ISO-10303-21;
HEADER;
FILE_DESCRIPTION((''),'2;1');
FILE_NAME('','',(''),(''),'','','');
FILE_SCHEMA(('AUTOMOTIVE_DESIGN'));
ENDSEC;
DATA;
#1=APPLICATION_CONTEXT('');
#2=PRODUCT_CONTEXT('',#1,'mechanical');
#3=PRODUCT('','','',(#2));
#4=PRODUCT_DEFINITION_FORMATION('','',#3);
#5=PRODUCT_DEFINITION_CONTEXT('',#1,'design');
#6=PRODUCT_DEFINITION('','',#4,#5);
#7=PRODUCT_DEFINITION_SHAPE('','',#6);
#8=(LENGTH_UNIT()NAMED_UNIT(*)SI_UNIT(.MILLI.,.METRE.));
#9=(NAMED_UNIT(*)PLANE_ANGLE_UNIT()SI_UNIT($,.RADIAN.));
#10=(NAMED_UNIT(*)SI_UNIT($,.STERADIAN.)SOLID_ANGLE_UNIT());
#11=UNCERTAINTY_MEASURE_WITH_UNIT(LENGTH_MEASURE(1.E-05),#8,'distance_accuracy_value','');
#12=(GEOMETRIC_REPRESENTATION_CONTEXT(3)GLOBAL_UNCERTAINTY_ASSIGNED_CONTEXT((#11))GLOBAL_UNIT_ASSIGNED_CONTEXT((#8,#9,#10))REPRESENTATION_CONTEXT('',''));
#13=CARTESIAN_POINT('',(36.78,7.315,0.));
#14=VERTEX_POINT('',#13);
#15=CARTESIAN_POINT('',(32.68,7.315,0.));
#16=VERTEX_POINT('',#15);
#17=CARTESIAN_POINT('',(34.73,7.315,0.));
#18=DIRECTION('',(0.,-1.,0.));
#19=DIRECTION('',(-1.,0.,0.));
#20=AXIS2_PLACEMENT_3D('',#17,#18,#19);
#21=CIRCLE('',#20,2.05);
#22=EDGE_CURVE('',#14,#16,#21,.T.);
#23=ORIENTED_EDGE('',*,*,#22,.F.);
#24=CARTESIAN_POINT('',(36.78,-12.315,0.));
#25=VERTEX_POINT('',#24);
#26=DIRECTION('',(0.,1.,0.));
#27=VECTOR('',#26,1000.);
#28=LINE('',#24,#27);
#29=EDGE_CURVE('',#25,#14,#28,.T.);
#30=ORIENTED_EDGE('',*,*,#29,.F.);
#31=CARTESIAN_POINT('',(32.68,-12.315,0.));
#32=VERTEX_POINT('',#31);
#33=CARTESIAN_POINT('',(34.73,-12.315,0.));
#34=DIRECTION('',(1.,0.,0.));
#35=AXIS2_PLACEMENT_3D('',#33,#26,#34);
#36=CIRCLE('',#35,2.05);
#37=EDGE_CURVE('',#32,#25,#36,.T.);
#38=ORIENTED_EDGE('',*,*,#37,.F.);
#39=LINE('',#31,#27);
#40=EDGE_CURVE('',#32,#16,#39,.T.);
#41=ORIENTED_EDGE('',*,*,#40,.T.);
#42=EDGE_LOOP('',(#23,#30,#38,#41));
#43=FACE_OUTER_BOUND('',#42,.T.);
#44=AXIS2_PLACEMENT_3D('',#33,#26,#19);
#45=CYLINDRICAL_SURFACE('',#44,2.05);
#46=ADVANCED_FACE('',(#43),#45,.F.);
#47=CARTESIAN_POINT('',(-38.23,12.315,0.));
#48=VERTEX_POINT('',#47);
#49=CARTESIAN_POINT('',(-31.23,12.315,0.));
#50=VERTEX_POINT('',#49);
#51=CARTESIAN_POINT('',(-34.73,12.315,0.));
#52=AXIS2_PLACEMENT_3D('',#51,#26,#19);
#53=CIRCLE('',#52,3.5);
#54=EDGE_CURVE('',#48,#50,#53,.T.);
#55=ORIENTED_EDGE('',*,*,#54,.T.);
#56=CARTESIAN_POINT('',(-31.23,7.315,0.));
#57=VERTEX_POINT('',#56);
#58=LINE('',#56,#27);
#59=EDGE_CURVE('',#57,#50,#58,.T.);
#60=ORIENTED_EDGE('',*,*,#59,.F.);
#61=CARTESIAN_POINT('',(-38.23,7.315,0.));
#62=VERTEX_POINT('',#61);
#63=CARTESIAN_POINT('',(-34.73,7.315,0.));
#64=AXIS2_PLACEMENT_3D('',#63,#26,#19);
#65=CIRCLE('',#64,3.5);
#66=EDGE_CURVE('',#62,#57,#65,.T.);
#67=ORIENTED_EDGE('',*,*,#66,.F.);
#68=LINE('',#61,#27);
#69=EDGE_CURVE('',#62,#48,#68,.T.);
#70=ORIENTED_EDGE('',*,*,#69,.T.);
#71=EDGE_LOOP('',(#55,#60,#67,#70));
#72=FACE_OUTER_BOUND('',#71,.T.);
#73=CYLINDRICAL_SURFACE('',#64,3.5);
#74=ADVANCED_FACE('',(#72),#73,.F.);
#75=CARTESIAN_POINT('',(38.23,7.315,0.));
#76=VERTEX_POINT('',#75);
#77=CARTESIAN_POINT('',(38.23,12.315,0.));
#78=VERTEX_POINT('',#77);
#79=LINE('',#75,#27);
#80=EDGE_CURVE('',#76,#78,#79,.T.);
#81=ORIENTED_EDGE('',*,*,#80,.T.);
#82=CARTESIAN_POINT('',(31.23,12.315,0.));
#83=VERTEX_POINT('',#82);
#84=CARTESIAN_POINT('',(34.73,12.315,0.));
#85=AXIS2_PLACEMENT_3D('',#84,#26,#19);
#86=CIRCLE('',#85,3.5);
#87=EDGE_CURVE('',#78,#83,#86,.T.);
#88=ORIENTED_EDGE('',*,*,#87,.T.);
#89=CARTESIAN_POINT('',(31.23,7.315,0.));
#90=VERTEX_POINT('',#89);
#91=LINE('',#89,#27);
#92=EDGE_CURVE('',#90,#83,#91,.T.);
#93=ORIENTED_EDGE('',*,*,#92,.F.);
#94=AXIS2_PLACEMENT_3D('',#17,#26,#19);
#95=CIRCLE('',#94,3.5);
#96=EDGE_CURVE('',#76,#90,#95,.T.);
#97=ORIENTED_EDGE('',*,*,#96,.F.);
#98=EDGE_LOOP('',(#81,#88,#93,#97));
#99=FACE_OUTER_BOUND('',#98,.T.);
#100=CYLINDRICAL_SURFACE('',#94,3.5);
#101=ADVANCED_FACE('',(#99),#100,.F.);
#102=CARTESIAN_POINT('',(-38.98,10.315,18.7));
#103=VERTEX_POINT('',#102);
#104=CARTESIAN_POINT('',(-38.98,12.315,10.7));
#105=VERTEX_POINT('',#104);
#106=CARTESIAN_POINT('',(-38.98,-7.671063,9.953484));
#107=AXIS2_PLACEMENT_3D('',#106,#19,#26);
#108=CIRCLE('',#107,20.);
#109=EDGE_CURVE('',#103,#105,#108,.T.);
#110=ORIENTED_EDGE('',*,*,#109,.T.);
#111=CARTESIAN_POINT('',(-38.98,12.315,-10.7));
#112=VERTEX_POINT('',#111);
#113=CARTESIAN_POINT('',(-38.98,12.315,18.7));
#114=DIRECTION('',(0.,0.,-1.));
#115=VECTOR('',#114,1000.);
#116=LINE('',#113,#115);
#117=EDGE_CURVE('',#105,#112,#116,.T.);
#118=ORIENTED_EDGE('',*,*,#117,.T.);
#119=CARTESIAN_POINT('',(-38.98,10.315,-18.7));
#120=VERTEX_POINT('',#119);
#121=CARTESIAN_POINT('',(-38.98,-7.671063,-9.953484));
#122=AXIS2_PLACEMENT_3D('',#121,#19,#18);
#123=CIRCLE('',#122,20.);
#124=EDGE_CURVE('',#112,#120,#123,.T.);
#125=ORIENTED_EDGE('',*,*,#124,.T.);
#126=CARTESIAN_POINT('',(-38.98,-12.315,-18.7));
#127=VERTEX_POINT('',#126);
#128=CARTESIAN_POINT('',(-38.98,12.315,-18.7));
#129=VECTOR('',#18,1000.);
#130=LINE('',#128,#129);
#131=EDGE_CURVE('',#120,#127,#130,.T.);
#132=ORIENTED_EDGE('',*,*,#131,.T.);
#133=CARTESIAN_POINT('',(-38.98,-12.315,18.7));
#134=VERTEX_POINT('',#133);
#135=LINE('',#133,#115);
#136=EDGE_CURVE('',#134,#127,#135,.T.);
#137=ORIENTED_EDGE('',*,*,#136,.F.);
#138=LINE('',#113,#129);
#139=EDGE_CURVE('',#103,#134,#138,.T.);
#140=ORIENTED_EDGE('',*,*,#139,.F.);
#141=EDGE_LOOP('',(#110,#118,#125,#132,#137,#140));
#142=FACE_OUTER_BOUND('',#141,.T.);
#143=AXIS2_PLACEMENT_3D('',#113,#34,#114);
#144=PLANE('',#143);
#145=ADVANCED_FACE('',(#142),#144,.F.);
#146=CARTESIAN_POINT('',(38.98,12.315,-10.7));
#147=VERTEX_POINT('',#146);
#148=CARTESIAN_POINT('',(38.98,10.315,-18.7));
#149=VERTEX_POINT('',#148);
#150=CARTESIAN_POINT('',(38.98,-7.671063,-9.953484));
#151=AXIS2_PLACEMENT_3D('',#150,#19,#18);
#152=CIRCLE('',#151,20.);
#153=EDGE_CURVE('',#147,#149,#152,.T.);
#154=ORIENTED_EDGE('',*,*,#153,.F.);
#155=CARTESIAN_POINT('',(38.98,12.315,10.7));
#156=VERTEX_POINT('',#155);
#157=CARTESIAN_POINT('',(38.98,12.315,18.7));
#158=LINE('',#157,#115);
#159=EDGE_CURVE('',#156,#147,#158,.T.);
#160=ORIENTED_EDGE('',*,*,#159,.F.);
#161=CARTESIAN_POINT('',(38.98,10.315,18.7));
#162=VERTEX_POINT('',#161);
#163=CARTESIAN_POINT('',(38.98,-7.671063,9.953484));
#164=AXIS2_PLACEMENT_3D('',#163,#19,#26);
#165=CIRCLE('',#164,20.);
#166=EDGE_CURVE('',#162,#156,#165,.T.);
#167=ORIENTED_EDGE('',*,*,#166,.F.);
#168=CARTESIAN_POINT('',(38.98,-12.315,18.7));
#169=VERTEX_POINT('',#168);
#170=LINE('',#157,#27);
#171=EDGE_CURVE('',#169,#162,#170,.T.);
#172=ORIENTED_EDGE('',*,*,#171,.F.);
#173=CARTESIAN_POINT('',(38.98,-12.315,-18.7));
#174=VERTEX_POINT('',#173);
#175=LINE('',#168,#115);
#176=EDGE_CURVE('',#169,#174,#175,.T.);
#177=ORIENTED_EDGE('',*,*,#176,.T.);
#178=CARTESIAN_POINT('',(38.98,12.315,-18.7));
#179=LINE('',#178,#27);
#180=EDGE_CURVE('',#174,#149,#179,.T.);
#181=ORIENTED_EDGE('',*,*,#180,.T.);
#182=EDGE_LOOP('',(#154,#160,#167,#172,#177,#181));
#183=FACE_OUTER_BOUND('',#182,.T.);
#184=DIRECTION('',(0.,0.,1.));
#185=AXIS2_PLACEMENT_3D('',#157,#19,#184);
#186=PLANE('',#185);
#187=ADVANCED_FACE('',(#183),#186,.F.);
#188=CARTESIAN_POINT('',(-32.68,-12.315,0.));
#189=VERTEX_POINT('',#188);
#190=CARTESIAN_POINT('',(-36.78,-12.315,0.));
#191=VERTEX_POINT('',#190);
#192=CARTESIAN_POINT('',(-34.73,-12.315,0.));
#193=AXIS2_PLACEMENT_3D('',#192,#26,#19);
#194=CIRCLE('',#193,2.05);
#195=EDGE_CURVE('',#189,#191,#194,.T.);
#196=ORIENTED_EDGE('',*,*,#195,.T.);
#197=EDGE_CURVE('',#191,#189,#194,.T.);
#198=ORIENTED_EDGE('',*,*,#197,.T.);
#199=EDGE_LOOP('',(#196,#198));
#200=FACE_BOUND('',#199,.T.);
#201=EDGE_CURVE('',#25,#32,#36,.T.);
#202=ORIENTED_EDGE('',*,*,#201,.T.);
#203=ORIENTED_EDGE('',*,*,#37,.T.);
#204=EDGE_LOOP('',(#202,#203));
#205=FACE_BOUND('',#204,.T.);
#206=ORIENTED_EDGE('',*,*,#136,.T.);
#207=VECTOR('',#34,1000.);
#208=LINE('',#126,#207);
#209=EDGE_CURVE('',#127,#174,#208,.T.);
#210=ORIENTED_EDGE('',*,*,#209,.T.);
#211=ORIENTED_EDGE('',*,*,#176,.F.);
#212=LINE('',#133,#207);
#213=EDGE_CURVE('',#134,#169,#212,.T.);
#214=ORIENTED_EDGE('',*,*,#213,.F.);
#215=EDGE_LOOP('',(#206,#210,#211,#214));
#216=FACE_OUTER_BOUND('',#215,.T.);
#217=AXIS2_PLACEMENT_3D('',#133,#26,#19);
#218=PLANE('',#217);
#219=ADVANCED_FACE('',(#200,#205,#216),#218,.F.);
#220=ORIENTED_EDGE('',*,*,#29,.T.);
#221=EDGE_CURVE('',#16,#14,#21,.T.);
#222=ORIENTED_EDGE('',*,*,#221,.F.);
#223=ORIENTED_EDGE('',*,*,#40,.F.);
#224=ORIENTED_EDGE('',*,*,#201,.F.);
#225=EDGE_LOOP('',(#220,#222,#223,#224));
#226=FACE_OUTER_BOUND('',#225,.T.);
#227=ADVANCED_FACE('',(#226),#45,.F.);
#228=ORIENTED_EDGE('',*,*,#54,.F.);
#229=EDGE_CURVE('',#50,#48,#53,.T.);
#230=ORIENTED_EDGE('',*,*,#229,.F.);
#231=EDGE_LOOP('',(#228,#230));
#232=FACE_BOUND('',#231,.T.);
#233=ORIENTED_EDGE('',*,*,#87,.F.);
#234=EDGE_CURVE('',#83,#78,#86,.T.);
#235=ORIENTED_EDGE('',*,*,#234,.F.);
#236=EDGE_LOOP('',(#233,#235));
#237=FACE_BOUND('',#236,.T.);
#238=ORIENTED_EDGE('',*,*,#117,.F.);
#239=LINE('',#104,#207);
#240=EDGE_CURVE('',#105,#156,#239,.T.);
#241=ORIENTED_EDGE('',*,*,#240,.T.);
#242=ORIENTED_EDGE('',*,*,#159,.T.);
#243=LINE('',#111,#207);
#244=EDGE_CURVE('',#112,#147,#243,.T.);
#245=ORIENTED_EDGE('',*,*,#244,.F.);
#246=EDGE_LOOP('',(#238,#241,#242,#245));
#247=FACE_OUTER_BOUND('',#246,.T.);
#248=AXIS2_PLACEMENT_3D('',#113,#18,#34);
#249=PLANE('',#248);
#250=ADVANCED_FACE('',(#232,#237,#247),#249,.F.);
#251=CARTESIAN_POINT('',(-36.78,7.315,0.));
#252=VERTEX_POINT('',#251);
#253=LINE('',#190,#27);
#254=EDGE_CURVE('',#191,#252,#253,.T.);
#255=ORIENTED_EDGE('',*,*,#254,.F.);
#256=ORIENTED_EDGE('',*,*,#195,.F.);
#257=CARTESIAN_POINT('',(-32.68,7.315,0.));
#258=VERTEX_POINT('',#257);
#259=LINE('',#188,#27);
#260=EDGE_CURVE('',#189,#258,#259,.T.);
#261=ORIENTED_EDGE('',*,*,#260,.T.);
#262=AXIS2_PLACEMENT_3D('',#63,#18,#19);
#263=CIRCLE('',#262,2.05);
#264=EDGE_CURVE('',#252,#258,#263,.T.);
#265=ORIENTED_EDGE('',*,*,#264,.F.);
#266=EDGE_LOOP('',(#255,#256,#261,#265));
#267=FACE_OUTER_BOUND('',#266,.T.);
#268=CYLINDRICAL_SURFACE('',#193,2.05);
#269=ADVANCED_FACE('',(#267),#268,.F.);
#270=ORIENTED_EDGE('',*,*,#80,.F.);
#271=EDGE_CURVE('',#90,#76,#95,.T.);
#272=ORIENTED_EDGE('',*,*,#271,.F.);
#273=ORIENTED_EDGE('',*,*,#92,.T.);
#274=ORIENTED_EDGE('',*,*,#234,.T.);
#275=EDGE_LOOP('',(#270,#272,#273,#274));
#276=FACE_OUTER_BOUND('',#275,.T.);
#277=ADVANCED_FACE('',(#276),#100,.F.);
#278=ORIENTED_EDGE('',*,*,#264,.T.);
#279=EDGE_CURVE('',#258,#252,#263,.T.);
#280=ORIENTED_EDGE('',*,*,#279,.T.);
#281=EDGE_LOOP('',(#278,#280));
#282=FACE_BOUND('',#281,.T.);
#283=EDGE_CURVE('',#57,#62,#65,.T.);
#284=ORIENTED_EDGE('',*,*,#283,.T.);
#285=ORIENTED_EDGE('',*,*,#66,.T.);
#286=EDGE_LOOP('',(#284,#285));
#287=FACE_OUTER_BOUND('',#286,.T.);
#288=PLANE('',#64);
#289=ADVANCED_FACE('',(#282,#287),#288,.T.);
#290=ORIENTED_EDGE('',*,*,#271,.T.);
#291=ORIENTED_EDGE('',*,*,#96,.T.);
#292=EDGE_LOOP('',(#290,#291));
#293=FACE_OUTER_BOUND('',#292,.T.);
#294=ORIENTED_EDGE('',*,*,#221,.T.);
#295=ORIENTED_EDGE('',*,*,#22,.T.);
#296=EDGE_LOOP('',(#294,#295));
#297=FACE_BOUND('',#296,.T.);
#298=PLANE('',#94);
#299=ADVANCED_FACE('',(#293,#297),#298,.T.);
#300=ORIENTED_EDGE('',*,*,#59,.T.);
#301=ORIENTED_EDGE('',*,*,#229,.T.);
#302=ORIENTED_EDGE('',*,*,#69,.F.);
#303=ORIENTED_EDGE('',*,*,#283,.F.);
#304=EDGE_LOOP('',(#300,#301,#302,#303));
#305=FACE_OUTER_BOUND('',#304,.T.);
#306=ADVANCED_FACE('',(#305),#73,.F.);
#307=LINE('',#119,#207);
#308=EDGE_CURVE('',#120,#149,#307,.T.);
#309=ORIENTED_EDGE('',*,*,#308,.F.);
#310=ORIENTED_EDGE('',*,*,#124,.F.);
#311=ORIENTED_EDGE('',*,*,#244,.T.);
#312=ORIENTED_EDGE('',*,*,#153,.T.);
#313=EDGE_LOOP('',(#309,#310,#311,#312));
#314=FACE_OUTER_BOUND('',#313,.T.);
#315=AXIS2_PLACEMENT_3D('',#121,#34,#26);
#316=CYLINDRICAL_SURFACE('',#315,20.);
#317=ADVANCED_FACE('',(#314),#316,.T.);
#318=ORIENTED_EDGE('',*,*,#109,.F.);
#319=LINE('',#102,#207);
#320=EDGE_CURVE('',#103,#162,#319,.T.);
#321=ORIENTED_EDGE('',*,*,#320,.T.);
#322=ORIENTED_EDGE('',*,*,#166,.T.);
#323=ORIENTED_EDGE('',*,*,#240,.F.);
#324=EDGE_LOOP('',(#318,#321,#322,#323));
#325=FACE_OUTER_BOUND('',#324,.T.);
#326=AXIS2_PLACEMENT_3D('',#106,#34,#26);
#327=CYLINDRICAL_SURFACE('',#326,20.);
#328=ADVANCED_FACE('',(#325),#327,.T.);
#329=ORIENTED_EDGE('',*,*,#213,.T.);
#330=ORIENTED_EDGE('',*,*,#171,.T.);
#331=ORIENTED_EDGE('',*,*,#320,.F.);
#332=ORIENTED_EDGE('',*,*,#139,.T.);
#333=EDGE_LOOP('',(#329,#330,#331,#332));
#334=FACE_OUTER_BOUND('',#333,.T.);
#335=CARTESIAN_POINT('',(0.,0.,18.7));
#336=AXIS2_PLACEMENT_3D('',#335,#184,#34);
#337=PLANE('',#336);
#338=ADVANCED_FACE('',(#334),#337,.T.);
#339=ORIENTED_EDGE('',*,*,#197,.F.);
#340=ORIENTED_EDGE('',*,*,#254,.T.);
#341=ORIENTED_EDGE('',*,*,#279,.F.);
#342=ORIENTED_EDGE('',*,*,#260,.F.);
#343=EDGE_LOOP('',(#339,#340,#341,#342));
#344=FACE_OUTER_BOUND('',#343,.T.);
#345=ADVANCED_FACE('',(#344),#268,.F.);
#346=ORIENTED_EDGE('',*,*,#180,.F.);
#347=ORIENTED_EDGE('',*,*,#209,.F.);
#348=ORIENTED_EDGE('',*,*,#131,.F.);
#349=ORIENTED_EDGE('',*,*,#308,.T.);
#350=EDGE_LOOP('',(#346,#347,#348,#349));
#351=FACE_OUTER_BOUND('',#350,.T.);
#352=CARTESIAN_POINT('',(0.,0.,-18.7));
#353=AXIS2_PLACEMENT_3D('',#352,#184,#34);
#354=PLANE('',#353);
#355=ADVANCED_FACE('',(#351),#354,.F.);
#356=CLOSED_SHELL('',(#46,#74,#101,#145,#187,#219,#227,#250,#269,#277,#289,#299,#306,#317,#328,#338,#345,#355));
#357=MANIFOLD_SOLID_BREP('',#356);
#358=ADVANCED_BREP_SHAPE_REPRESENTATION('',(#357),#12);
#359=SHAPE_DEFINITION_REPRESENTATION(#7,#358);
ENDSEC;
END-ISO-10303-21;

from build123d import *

# Parameters (mm, degrees)
SKETCH_1_W          = 77.96
SKETCH_1_H          = 24.63
EXTRUDE_1_DEPTH     = 18.7
CUT_EXTRUDE_1_DEPTH = 82.111718173
SKETCH_3_R          = 2.05
CUT_EXTRUDE_2_DEPTH = 50.757082913
SKETCH_4_R          = 3.5
CUT_EXTRUDE_3_DEPTH = 5


with BuildPart() as part:
    # 草图1 → 凸台-拉伸1 (new, symmetric)
    with BuildSketch(Plane.XY):
        Rectangle(SKETCH_1_W, SKETCH_1_H)
    extrude(amount=EXTRUDE_1_DEPTH, both=True)

    # 草图2 → 切除-拉伸1 (cut, through all)
    with BuildSketch(Plane(origin=(38.98, 0, 0), x_dir=(0, 0, -1), z_dir=(1, 0, 0))):
        with BuildLine():
            Line((-18.7, 10.315), (-18.7, 12.315))
            Line((-18.7, 12.315), (-10.7, 12.315))
            ThreePointArc((-10.7, 12.315), (-14.804196751, 11.731787003), (-18.7, 10.315))
        make_face()
        with BuildLine():
            Line((18.7, 12.315), (10.7, 12.315))
            ThreePointArc((10.7, 12.315), (14.804196751, 11.731787003), (18.7, 10.315))
            Line((18.7, 10.315), (18.7, 12.315))
        make_face()
    extrude(amount=-CUT_EXTRUDE_1_DEPTH, mode=Mode.SUBTRACT)

    # 草图3 → 切除-拉伸2 (cut, through all)
    with BuildSketch(Plane(origin=(0, 12.315, 0), x_dir=(1, 0, 0), z_dir=(0, 1, 0))):
        with Locations(Location((-34.73, 0, 0), (0, 0, 180))):
            Circle(SKETCH_3_R)
        with Locations((34.73, 0)):
            Circle(SKETCH_3_R)
    extrude(amount=-CUT_EXTRUDE_2_DEPTH, mode=Mode.SUBTRACT)

    # 草图4 → 切除-拉伸3 (cut)
    with BuildSketch(Plane(origin=(0, 12.315, 0), x_dir=(1, 0, 0), z_dir=(0, 1, 0))):
        with Locations(Location((-34.73, 0, 0), (0, 0, 180))):
            Circle(SKETCH_4_R)
        with Locations(Location((34.73, 0, 0), (0, 0, 180))):
            Circle(SKETCH_4_R)
    extrude(amount=-CUT_EXTRUDE_3_DEPTH, mode=Mode.SUBTRACT)


solid = part.part
